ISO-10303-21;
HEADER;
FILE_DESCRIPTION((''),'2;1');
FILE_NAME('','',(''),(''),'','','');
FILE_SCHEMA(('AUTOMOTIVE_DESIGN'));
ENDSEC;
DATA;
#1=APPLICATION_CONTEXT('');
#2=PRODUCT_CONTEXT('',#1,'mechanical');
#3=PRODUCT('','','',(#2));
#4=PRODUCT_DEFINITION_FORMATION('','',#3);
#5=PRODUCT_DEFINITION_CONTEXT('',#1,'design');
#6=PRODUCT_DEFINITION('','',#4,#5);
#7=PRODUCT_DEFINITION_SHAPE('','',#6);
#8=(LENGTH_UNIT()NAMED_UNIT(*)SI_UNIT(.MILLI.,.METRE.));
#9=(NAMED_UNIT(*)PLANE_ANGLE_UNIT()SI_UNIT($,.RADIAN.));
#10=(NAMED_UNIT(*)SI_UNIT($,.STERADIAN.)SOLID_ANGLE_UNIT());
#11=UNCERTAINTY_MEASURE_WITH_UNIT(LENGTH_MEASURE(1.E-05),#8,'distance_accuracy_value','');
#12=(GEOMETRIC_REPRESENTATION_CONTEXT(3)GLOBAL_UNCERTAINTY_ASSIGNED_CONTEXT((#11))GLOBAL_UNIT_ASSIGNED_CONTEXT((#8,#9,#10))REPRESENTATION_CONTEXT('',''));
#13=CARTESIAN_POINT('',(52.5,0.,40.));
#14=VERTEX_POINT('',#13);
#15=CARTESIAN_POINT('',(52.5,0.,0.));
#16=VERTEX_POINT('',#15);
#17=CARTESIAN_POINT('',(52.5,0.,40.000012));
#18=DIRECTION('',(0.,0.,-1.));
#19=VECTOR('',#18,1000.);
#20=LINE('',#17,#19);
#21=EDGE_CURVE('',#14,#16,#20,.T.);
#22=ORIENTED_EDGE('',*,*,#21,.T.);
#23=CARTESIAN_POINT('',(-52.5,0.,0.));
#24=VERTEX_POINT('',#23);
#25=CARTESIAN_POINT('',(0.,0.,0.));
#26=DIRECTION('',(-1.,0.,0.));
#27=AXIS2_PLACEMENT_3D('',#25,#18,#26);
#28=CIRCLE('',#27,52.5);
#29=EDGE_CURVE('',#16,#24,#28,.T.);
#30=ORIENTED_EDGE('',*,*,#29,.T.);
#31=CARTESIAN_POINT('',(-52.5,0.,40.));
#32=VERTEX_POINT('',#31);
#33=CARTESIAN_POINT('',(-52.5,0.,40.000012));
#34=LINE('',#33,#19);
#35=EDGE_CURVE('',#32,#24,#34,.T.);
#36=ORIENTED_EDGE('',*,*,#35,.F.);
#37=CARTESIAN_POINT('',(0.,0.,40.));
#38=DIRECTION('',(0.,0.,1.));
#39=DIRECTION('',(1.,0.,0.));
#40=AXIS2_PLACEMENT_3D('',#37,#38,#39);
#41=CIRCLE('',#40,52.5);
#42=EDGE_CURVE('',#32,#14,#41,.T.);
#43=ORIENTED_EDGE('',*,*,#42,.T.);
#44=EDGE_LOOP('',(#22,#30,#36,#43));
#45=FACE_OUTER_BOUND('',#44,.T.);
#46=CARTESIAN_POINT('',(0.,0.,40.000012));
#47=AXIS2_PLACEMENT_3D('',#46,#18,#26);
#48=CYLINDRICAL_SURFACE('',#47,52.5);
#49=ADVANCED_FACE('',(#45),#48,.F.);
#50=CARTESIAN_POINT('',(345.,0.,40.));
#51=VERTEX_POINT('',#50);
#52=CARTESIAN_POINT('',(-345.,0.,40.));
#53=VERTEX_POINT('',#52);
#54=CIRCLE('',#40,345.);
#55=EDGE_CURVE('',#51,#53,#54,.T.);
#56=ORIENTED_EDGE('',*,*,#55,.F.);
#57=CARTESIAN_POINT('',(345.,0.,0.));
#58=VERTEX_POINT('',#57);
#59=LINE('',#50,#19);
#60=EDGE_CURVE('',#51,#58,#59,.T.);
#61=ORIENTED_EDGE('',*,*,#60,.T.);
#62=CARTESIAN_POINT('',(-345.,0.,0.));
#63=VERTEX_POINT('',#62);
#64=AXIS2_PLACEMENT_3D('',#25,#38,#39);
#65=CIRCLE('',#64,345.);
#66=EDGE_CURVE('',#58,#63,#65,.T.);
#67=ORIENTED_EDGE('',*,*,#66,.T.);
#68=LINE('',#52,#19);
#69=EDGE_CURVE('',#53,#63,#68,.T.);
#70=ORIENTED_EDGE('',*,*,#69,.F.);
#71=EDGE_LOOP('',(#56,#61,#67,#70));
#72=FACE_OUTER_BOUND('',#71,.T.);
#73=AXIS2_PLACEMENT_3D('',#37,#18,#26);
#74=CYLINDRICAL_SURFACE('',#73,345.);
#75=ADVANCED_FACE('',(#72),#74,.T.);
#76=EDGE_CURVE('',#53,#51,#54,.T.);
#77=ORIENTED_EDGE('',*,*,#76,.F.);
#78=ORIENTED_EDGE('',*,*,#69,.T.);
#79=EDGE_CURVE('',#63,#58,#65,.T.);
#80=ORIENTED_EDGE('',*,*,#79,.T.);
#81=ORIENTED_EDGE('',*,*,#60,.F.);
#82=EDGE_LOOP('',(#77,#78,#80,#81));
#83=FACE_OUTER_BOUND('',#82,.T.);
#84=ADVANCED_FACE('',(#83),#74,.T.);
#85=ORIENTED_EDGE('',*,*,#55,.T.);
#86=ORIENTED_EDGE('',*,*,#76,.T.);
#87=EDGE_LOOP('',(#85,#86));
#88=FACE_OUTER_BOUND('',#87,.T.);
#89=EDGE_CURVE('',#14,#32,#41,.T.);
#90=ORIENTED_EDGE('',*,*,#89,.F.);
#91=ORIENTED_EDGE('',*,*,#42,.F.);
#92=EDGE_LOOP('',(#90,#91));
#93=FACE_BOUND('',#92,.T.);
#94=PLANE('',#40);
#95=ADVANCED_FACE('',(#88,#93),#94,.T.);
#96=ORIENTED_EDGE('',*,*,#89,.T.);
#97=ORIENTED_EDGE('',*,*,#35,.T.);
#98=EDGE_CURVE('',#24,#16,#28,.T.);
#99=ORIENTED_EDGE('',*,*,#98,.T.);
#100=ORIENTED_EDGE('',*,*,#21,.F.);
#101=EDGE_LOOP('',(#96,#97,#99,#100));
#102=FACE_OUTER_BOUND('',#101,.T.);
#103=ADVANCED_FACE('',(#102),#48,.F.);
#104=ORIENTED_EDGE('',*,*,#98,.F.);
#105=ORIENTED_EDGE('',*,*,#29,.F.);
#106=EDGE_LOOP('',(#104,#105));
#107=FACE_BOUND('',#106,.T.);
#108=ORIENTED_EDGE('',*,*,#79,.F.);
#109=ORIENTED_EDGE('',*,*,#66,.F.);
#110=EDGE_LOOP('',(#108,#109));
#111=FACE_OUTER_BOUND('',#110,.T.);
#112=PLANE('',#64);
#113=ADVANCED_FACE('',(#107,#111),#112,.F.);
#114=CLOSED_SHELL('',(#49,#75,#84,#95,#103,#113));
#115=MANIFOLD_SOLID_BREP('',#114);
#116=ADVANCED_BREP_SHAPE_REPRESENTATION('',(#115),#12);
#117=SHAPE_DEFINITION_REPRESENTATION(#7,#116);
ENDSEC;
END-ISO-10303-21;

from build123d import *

# Parameters (mm, degrees)
SKETCH1_R               = 345
BOSS_EXTRUDE1_DEPTH     = 40
CUT_EXTRUDE3_DEPTH      = 490.540600972
CUT_EXTRUDE3_DEPTH_BACK = 490.540600972
SKETCH8_R               = 52.5


with BuildPart() as part:
    # Sketch1 → Boss-Extrude1 (new body)
    with BuildSketch(Plane.XY):
        Circle(SKETCH1_R)
    extrude(amount=BOSS_EXTRUDE1_DEPTH)

    # Sketch8 → Cut-Extrude3 (cut, two sides: drawn at the far end of the back side and taken through both)
    with BuildSketch(Plane(origin=(0, 0, 40), x_dir=(-1, 0, 0), z_dir=(0, 0, -1)).offset(-CUT_EXTRUDE3_DEPTH_BACK)):
        Circle(SKETCH8_R)
    extrude(amount=CUT_EXTRUDE3_DEPTH + CUT_EXTRUDE3_DEPTH_BACK, mode=Mode.SUBTRACT)


solid = part.part
